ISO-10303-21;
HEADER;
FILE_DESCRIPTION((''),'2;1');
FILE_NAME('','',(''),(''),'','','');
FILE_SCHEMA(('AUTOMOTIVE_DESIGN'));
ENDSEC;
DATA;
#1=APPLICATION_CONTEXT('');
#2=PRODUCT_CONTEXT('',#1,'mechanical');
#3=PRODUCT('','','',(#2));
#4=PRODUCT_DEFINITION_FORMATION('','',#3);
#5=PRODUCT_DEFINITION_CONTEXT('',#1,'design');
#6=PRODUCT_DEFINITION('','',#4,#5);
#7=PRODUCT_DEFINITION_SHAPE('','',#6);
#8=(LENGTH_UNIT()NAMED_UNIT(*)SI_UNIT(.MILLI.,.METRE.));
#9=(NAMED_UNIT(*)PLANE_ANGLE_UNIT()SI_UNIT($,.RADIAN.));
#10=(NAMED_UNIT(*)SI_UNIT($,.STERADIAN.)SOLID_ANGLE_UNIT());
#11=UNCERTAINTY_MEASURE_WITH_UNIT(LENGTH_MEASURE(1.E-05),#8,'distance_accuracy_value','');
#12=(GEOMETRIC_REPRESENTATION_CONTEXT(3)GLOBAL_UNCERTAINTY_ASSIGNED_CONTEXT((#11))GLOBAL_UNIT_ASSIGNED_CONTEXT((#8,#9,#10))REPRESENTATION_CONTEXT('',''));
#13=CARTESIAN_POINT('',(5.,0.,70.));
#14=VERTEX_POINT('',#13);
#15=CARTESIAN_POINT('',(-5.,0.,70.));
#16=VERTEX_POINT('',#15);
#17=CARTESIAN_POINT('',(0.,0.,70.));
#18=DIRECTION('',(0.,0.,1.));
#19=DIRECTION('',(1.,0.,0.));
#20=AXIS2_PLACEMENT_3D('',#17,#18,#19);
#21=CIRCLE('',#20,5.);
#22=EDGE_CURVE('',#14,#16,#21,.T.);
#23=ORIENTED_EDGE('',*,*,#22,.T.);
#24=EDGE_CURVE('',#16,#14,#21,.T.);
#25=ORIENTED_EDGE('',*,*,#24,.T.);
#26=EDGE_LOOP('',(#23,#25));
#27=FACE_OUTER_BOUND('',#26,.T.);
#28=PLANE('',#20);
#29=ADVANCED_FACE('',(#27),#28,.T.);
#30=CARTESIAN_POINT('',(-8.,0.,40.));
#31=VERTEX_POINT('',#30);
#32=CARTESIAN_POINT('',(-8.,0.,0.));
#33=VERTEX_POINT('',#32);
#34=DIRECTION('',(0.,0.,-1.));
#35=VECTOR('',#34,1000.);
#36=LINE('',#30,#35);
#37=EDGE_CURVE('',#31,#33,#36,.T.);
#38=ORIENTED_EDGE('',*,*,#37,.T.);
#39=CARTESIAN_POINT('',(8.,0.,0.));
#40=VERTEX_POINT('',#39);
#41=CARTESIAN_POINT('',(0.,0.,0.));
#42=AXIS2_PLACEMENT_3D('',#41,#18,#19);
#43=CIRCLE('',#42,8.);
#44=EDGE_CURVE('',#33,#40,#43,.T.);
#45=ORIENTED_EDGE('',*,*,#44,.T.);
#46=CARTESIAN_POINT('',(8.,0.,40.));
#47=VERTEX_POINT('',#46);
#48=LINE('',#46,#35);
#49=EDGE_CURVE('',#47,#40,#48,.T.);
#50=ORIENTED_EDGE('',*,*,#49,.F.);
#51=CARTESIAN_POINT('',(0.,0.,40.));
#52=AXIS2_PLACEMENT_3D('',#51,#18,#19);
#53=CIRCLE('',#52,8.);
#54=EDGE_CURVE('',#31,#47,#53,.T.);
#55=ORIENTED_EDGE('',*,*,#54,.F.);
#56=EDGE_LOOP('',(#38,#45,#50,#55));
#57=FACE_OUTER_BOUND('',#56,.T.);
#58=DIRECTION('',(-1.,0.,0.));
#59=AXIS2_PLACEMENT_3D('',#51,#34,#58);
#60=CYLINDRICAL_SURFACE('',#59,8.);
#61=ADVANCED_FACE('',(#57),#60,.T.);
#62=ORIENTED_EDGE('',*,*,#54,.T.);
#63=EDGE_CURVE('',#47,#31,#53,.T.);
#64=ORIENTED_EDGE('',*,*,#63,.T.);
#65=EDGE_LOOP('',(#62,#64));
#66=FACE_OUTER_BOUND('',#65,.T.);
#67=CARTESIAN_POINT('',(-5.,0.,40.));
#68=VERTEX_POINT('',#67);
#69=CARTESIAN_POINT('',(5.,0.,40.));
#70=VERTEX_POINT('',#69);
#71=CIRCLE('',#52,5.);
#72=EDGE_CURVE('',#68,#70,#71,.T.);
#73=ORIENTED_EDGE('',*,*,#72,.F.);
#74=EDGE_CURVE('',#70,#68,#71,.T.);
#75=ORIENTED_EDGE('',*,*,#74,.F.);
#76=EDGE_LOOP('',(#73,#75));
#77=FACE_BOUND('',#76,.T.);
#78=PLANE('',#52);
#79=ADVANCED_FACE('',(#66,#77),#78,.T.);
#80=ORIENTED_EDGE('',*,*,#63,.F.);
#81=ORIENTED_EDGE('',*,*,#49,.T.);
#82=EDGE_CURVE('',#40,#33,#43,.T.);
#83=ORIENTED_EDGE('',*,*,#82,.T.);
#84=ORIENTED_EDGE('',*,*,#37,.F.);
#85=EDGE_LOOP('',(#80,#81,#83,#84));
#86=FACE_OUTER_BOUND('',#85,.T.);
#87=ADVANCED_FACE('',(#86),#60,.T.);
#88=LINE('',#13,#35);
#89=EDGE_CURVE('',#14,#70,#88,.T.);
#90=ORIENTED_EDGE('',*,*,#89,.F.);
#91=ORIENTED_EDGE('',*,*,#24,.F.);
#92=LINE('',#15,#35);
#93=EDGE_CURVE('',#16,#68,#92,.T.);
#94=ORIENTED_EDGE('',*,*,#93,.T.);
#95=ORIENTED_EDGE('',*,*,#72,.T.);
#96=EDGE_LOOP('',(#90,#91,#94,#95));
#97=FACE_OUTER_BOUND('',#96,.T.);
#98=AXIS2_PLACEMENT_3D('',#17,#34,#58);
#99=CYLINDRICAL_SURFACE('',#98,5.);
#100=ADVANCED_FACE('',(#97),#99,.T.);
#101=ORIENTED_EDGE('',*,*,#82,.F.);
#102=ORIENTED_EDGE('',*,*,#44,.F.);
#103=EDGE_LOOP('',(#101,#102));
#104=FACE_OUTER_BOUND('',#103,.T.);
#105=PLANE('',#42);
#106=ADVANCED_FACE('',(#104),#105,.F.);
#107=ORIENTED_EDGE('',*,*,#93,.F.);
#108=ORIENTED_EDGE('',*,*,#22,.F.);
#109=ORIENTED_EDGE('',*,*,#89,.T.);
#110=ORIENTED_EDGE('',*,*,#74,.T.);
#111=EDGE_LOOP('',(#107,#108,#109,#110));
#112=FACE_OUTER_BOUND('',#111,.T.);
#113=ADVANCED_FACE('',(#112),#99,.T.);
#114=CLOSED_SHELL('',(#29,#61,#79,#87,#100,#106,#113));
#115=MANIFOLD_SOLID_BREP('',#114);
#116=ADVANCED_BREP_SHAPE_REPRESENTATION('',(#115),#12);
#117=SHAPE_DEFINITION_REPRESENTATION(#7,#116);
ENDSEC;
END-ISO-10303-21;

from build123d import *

# Parameters (mm, degrees)
SKETCH1_R           = 8
BOSS_EXTRUDE1_DEPTH = 40
SKETCH2_R           = 5
BOSS_EXTRUDE2_DEPTH = 30


with BuildPart() as part:
    # Sketch1 → Boss-Extrude1 (new body)
    with BuildSketch(Plane.XY):
        Circle(SKETCH1_R)
    extrude(amount=BOSS_EXTRUDE1_DEPTH)

    # Sketch2 → Boss-Extrude2 (add)
    with BuildSketch(Plane.XY.offset(40)):
        Circle(SKETCH2_R)
    extrude(amount=BOSS_EXTRUDE2_DEPTH)


solid = part.part
